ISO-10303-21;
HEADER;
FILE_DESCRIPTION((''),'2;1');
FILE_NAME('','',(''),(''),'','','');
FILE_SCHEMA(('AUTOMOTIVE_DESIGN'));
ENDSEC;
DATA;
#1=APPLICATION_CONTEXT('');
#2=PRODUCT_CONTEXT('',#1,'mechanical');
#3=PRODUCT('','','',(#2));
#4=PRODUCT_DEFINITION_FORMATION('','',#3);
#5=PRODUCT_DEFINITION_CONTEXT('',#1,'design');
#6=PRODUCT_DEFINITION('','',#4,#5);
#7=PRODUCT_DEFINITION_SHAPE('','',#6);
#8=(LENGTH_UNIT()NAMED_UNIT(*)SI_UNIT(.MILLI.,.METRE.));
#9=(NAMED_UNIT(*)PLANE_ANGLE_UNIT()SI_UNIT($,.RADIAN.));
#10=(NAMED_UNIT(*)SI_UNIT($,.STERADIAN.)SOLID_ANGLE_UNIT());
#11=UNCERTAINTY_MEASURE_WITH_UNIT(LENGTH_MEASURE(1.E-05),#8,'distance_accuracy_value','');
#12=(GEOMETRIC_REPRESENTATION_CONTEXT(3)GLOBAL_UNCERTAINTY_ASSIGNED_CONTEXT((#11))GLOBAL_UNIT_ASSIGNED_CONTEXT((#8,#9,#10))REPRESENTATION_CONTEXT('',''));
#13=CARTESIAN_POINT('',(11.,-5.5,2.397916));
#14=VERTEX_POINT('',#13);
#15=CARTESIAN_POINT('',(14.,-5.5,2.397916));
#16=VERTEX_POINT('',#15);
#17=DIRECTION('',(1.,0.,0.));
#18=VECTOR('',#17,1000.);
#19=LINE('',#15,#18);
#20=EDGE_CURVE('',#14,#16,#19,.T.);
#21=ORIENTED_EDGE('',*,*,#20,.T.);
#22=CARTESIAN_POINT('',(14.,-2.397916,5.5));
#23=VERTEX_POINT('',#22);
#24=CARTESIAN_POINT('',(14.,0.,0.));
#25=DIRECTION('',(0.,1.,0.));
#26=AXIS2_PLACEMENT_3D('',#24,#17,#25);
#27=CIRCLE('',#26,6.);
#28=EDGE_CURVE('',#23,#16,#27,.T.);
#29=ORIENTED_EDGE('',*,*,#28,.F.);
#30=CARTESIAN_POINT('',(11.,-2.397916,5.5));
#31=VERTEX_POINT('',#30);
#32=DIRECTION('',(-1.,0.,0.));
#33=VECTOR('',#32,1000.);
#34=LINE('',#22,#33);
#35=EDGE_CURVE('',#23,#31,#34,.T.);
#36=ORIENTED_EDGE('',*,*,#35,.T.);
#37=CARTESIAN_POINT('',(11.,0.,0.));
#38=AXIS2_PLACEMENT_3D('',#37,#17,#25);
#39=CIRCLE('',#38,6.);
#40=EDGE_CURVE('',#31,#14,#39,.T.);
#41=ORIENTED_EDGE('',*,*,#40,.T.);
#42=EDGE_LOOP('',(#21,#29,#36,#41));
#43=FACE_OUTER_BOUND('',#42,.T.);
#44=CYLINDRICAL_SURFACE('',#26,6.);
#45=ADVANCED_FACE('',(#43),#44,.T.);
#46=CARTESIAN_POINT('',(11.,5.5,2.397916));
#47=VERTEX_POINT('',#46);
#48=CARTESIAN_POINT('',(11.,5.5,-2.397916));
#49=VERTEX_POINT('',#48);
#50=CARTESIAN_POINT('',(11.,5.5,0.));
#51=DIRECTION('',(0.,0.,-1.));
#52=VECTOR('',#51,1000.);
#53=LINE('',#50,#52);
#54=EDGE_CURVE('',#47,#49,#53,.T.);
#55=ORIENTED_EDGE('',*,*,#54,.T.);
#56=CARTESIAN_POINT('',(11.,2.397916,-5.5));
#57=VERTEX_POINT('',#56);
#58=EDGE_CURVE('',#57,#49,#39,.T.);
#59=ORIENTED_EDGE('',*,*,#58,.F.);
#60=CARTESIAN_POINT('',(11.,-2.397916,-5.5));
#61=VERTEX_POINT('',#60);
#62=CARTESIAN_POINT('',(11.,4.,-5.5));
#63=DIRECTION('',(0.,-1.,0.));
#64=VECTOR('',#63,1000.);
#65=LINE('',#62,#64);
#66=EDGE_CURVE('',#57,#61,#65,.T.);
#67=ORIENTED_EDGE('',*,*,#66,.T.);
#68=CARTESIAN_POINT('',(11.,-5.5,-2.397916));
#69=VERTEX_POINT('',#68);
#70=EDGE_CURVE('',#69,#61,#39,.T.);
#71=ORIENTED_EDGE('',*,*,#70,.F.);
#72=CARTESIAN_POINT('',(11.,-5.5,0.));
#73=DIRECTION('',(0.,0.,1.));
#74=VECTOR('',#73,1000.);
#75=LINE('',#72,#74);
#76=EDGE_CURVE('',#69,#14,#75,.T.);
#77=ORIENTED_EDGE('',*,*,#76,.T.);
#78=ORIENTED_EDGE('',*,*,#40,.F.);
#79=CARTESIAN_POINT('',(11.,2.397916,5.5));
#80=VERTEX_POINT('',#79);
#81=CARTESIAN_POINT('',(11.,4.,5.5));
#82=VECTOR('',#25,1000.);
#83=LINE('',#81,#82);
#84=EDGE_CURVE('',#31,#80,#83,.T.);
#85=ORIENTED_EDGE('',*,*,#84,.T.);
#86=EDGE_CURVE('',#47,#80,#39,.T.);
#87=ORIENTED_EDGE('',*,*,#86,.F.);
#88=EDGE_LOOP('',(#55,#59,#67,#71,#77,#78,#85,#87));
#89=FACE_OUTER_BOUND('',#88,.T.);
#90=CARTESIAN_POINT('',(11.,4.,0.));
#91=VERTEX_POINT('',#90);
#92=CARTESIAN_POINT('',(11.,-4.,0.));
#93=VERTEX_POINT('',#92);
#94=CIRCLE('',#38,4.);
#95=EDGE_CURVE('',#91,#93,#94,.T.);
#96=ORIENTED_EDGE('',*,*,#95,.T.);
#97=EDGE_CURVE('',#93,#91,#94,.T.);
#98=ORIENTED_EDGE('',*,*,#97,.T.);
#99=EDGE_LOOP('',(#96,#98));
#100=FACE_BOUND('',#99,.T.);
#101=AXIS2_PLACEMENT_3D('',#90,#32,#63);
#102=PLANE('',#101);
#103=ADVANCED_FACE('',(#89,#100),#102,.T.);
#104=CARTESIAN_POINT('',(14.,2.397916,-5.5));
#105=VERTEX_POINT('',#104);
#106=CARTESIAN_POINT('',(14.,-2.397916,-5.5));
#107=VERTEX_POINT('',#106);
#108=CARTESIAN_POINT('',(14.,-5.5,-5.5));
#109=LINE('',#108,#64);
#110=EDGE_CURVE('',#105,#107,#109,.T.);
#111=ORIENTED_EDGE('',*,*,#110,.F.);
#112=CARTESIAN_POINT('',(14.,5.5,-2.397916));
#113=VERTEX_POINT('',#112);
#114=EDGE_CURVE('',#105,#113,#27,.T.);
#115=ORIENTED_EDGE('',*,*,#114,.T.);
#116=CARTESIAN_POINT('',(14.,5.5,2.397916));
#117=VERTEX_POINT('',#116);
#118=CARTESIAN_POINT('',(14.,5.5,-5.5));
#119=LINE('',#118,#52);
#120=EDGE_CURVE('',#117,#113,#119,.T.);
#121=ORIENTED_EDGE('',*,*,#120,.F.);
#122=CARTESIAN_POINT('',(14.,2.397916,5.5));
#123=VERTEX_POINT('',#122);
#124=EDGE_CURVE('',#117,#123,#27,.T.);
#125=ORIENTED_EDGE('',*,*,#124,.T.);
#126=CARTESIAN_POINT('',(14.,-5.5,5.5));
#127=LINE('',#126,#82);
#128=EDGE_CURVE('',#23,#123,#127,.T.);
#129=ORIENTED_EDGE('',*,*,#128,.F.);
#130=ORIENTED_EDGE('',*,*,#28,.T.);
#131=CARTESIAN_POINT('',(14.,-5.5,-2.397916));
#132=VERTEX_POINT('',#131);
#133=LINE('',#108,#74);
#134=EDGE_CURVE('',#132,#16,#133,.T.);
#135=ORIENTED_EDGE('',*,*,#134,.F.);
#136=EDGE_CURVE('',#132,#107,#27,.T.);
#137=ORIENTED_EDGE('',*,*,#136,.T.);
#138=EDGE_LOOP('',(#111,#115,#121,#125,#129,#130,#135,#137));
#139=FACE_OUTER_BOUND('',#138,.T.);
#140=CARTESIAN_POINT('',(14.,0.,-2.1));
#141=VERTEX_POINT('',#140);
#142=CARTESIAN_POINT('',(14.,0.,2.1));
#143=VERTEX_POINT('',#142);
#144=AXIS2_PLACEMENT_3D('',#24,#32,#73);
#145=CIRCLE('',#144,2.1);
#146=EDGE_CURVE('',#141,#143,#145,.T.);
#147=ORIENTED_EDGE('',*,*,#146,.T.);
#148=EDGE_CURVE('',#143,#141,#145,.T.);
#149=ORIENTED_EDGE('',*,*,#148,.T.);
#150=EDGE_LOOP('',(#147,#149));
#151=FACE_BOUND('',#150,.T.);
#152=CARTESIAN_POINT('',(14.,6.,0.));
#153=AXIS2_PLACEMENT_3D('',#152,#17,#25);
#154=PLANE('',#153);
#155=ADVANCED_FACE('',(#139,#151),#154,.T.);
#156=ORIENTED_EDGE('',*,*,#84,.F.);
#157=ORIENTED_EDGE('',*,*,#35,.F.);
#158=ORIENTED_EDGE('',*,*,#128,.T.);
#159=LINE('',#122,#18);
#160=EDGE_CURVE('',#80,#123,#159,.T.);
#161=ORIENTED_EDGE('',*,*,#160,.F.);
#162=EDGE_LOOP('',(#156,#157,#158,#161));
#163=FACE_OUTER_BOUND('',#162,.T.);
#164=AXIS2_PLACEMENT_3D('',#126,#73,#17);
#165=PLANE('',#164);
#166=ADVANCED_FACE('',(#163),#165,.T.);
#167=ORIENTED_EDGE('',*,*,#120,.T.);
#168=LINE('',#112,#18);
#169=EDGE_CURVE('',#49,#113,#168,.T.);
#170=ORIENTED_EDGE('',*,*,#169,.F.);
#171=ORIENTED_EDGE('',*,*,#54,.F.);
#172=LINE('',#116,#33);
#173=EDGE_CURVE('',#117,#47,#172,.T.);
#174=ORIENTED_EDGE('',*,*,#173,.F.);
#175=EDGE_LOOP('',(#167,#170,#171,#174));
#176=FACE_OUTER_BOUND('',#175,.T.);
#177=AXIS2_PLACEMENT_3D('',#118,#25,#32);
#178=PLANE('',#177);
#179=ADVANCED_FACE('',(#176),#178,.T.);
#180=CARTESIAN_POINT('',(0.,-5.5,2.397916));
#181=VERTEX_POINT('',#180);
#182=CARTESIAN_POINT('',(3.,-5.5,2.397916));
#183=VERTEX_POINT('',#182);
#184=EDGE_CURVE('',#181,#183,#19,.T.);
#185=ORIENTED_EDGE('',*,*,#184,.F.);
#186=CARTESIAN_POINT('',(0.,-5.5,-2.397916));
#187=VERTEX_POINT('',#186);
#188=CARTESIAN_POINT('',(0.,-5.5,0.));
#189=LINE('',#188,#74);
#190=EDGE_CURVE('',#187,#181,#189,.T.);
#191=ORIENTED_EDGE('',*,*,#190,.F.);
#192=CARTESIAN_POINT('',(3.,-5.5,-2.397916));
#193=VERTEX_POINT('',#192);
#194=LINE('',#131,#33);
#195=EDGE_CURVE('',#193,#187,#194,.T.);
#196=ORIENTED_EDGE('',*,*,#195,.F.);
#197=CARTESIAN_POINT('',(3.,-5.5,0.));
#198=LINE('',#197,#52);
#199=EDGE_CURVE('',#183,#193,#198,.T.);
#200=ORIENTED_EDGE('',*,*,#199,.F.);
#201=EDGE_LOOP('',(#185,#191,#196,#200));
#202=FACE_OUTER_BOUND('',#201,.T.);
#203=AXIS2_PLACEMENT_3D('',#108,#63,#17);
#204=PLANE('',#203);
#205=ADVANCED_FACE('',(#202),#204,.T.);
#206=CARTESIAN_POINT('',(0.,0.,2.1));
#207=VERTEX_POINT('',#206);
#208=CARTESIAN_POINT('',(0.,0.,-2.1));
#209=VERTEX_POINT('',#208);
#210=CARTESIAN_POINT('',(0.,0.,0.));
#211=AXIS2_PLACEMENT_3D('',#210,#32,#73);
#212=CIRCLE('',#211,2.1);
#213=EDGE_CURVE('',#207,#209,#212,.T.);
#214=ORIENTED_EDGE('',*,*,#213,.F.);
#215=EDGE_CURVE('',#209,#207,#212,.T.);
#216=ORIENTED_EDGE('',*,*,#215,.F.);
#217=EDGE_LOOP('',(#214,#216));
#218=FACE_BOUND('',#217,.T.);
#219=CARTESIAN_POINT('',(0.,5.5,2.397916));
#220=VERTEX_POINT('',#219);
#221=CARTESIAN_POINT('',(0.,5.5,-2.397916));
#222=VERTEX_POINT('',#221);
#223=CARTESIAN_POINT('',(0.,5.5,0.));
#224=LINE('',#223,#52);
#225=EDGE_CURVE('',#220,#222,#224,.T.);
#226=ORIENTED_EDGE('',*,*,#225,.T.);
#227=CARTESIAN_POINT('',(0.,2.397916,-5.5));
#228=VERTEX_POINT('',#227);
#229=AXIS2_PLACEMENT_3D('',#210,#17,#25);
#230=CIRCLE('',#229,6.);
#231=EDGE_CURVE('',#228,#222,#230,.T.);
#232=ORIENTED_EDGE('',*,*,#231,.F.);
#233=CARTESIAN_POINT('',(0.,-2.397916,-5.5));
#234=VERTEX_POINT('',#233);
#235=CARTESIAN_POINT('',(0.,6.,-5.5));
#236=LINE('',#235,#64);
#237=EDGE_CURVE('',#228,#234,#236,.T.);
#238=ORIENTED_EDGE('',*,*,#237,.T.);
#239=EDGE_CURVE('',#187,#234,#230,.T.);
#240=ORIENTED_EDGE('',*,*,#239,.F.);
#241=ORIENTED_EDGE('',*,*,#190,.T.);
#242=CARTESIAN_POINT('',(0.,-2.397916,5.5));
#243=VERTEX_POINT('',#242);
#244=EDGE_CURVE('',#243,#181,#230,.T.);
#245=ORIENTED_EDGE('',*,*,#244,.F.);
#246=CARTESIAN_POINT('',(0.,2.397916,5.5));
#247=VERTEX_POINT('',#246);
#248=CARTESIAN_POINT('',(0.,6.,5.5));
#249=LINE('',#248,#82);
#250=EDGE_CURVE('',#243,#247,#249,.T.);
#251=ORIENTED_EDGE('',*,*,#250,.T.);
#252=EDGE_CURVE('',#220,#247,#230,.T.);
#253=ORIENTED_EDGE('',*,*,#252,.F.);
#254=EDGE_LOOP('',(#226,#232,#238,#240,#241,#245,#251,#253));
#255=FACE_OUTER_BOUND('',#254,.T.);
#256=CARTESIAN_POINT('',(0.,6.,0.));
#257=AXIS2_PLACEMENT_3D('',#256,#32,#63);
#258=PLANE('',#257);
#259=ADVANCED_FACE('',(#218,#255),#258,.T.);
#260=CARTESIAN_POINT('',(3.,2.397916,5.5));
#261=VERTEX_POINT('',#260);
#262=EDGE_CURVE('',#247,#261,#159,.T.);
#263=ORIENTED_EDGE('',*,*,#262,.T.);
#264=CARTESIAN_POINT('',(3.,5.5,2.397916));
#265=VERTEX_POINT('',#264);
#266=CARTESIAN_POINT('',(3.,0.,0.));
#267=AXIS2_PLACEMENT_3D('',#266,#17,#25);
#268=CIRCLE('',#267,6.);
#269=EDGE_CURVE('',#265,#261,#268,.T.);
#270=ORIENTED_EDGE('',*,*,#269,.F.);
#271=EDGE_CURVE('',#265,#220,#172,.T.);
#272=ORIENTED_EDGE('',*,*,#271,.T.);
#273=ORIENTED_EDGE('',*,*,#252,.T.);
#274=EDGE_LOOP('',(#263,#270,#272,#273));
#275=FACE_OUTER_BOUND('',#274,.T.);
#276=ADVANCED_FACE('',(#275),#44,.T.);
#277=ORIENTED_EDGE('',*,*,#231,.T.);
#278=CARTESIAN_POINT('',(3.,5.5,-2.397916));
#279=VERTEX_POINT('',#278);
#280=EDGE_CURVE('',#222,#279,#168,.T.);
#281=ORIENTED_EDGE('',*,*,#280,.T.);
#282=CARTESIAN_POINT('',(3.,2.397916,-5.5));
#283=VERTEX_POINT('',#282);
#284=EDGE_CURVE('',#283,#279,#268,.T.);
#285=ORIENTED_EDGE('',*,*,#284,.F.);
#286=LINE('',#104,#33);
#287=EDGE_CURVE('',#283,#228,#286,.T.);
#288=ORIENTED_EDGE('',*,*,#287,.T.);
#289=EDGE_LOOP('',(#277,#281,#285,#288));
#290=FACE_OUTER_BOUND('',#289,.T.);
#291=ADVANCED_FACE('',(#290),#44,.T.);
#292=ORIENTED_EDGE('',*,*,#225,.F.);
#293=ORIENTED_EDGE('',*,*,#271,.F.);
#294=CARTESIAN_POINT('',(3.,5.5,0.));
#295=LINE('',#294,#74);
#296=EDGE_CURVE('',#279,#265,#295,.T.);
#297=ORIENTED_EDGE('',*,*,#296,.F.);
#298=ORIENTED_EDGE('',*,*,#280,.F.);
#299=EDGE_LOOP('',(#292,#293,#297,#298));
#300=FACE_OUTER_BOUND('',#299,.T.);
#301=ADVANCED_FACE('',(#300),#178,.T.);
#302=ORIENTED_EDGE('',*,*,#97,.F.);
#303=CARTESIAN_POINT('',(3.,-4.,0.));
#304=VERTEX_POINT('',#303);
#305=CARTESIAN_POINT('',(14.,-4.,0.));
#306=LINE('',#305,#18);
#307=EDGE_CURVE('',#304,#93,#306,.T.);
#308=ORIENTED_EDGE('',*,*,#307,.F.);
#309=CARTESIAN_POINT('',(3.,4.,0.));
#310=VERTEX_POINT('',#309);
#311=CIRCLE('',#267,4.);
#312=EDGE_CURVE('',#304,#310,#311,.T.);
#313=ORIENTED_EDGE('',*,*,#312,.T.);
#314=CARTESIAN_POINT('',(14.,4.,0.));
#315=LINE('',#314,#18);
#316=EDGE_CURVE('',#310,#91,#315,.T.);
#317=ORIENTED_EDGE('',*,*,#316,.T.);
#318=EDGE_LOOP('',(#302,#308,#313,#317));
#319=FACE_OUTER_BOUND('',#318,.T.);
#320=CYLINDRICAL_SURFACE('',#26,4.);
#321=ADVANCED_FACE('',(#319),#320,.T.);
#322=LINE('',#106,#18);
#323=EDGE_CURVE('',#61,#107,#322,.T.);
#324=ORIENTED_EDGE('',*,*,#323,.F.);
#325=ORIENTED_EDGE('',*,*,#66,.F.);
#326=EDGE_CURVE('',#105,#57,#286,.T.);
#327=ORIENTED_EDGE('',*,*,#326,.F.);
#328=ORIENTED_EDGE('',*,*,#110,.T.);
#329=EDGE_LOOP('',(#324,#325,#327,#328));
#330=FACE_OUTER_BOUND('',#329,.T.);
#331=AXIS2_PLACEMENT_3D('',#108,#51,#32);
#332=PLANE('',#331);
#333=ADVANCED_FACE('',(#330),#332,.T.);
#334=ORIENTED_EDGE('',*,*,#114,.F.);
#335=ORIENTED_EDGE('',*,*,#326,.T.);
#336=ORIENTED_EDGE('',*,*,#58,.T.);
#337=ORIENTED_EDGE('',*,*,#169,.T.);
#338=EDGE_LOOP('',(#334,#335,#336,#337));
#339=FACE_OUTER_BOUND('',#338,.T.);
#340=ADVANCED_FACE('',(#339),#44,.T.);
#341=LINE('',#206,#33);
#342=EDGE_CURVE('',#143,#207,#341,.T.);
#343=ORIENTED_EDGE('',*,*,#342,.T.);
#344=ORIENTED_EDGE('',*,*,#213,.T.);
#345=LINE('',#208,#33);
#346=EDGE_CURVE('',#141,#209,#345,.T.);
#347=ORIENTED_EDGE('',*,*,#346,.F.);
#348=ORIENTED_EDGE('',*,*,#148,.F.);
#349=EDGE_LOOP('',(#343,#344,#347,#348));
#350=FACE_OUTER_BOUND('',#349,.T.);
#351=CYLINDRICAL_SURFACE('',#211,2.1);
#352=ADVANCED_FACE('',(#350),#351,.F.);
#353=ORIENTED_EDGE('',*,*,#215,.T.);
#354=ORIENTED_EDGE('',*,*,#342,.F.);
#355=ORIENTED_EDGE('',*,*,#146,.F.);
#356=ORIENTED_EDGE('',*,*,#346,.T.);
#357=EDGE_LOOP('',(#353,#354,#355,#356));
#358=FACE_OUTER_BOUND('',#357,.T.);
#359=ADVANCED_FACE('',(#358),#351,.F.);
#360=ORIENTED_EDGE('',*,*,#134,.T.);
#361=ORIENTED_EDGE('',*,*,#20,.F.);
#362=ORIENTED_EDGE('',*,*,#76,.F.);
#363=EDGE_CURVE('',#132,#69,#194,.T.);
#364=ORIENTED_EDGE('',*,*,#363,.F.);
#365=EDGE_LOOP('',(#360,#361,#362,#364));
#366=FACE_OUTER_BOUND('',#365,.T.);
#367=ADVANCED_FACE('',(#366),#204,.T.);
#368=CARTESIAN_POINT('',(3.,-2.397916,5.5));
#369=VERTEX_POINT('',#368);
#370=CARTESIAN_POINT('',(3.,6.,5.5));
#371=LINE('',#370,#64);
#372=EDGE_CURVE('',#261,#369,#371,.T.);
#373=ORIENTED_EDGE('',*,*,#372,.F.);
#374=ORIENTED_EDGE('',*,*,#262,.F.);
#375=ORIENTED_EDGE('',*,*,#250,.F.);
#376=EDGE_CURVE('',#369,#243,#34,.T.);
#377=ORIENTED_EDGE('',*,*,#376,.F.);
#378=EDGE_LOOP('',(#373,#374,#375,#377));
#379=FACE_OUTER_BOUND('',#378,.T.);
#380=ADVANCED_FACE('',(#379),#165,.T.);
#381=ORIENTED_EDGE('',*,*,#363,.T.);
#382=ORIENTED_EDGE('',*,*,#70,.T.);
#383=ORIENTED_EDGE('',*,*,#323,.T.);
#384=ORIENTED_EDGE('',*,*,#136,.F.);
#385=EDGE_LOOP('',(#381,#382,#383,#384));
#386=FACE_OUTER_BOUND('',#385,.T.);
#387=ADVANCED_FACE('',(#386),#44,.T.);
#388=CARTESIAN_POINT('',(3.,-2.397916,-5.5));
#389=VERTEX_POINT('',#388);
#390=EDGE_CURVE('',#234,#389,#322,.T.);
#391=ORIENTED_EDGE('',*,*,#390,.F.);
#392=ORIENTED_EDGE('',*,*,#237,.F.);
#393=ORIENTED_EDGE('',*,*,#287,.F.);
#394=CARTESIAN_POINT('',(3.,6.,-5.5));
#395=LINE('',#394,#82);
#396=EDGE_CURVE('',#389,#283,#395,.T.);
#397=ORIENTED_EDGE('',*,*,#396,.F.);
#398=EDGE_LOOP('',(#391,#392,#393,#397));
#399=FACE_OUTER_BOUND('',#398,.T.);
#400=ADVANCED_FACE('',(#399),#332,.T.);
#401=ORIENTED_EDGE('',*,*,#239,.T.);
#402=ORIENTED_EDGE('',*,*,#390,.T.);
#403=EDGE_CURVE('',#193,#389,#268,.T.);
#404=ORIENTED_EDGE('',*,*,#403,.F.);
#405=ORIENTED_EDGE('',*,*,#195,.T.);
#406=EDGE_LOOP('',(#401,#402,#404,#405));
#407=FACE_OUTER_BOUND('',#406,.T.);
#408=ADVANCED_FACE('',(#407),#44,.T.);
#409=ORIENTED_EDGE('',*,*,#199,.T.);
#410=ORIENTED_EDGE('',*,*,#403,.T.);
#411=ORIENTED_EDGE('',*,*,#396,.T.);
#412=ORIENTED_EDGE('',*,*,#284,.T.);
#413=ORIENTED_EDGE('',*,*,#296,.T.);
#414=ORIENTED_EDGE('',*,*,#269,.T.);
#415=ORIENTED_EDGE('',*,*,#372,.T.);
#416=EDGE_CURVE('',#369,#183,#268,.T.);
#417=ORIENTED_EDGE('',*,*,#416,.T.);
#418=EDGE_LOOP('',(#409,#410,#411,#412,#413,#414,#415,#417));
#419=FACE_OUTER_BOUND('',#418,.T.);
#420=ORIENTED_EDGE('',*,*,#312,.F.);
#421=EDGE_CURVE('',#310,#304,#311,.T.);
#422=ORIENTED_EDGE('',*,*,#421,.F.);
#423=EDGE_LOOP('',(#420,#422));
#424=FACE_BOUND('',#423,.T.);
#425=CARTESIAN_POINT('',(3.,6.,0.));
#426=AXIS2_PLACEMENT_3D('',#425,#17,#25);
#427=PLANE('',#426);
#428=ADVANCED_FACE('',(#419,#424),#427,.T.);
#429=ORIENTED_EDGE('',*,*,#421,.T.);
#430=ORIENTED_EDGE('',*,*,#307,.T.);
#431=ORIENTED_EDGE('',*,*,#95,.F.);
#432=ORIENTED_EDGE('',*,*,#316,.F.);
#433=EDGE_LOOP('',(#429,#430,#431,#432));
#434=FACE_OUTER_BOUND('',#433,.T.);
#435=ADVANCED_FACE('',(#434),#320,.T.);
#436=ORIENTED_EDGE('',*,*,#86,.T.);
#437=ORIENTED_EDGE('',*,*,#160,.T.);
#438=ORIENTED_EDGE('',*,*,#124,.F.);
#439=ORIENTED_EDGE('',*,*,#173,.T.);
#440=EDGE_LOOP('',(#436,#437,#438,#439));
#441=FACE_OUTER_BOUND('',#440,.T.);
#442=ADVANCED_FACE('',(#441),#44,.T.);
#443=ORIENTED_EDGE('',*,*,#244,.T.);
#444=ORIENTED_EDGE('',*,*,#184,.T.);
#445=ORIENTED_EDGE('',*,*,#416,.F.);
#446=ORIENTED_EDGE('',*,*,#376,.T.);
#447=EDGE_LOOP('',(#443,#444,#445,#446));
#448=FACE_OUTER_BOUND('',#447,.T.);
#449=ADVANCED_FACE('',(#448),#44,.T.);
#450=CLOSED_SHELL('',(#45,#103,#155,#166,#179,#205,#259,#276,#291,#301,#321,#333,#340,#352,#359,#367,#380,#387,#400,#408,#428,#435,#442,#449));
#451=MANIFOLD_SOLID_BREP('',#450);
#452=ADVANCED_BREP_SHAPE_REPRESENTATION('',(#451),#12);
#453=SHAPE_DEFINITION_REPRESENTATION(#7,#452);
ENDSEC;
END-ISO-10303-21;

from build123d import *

# Parameters (mm, degrees)
M5_TAPPED_HOLE1_D   = 4.2
SKETCH4_OUTSIDE_W   = 18.4
SKETCH4_OUTSIDE_H   = 18.4
SKETCH4_OUTSIDE_W_2 = 11
SKETCH4_OUTSIDE_H_2 = 11
CUT_EXTRUDE1_DEPTH  = 17.370705544


with BuildPart() as part:
    # Sketch1 → Revolve1 (revolve)
    with BuildSketch(Plane.XY):
        Polygon((0, 6), (0, 0), (14, 0), (14, 6), (11, 6), (11, 4), (3, 4), (3, 6), align=None)
    revolve(axis=Axis((14, 0, 0), (-1, 0, 0)))

    # M5 Tapped Hole1 (through all)
    with Locations(Plane.ZY):
        with Locations((0, 0)):
            Hole(M5_TAPPED_HOLE1_D / 2)

    # Sketch4 outside → Cut-Extrude1 (cut, through all)
    with BuildSketch(Plane.ZY):
        Rectangle(SKETCH4_OUTSIDE_W, SKETCH4_OUTSIDE_H)
        Rectangle(SKETCH4_OUTSIDE_W_2, SKETCH4_OUTSIDE_H_2, mode=Mode.SUBTRACT)
    extrude(amount=-CUT_EXTRUDE1_DEPTH, mode=Mode.SUBTRACT)


solid = part.part
